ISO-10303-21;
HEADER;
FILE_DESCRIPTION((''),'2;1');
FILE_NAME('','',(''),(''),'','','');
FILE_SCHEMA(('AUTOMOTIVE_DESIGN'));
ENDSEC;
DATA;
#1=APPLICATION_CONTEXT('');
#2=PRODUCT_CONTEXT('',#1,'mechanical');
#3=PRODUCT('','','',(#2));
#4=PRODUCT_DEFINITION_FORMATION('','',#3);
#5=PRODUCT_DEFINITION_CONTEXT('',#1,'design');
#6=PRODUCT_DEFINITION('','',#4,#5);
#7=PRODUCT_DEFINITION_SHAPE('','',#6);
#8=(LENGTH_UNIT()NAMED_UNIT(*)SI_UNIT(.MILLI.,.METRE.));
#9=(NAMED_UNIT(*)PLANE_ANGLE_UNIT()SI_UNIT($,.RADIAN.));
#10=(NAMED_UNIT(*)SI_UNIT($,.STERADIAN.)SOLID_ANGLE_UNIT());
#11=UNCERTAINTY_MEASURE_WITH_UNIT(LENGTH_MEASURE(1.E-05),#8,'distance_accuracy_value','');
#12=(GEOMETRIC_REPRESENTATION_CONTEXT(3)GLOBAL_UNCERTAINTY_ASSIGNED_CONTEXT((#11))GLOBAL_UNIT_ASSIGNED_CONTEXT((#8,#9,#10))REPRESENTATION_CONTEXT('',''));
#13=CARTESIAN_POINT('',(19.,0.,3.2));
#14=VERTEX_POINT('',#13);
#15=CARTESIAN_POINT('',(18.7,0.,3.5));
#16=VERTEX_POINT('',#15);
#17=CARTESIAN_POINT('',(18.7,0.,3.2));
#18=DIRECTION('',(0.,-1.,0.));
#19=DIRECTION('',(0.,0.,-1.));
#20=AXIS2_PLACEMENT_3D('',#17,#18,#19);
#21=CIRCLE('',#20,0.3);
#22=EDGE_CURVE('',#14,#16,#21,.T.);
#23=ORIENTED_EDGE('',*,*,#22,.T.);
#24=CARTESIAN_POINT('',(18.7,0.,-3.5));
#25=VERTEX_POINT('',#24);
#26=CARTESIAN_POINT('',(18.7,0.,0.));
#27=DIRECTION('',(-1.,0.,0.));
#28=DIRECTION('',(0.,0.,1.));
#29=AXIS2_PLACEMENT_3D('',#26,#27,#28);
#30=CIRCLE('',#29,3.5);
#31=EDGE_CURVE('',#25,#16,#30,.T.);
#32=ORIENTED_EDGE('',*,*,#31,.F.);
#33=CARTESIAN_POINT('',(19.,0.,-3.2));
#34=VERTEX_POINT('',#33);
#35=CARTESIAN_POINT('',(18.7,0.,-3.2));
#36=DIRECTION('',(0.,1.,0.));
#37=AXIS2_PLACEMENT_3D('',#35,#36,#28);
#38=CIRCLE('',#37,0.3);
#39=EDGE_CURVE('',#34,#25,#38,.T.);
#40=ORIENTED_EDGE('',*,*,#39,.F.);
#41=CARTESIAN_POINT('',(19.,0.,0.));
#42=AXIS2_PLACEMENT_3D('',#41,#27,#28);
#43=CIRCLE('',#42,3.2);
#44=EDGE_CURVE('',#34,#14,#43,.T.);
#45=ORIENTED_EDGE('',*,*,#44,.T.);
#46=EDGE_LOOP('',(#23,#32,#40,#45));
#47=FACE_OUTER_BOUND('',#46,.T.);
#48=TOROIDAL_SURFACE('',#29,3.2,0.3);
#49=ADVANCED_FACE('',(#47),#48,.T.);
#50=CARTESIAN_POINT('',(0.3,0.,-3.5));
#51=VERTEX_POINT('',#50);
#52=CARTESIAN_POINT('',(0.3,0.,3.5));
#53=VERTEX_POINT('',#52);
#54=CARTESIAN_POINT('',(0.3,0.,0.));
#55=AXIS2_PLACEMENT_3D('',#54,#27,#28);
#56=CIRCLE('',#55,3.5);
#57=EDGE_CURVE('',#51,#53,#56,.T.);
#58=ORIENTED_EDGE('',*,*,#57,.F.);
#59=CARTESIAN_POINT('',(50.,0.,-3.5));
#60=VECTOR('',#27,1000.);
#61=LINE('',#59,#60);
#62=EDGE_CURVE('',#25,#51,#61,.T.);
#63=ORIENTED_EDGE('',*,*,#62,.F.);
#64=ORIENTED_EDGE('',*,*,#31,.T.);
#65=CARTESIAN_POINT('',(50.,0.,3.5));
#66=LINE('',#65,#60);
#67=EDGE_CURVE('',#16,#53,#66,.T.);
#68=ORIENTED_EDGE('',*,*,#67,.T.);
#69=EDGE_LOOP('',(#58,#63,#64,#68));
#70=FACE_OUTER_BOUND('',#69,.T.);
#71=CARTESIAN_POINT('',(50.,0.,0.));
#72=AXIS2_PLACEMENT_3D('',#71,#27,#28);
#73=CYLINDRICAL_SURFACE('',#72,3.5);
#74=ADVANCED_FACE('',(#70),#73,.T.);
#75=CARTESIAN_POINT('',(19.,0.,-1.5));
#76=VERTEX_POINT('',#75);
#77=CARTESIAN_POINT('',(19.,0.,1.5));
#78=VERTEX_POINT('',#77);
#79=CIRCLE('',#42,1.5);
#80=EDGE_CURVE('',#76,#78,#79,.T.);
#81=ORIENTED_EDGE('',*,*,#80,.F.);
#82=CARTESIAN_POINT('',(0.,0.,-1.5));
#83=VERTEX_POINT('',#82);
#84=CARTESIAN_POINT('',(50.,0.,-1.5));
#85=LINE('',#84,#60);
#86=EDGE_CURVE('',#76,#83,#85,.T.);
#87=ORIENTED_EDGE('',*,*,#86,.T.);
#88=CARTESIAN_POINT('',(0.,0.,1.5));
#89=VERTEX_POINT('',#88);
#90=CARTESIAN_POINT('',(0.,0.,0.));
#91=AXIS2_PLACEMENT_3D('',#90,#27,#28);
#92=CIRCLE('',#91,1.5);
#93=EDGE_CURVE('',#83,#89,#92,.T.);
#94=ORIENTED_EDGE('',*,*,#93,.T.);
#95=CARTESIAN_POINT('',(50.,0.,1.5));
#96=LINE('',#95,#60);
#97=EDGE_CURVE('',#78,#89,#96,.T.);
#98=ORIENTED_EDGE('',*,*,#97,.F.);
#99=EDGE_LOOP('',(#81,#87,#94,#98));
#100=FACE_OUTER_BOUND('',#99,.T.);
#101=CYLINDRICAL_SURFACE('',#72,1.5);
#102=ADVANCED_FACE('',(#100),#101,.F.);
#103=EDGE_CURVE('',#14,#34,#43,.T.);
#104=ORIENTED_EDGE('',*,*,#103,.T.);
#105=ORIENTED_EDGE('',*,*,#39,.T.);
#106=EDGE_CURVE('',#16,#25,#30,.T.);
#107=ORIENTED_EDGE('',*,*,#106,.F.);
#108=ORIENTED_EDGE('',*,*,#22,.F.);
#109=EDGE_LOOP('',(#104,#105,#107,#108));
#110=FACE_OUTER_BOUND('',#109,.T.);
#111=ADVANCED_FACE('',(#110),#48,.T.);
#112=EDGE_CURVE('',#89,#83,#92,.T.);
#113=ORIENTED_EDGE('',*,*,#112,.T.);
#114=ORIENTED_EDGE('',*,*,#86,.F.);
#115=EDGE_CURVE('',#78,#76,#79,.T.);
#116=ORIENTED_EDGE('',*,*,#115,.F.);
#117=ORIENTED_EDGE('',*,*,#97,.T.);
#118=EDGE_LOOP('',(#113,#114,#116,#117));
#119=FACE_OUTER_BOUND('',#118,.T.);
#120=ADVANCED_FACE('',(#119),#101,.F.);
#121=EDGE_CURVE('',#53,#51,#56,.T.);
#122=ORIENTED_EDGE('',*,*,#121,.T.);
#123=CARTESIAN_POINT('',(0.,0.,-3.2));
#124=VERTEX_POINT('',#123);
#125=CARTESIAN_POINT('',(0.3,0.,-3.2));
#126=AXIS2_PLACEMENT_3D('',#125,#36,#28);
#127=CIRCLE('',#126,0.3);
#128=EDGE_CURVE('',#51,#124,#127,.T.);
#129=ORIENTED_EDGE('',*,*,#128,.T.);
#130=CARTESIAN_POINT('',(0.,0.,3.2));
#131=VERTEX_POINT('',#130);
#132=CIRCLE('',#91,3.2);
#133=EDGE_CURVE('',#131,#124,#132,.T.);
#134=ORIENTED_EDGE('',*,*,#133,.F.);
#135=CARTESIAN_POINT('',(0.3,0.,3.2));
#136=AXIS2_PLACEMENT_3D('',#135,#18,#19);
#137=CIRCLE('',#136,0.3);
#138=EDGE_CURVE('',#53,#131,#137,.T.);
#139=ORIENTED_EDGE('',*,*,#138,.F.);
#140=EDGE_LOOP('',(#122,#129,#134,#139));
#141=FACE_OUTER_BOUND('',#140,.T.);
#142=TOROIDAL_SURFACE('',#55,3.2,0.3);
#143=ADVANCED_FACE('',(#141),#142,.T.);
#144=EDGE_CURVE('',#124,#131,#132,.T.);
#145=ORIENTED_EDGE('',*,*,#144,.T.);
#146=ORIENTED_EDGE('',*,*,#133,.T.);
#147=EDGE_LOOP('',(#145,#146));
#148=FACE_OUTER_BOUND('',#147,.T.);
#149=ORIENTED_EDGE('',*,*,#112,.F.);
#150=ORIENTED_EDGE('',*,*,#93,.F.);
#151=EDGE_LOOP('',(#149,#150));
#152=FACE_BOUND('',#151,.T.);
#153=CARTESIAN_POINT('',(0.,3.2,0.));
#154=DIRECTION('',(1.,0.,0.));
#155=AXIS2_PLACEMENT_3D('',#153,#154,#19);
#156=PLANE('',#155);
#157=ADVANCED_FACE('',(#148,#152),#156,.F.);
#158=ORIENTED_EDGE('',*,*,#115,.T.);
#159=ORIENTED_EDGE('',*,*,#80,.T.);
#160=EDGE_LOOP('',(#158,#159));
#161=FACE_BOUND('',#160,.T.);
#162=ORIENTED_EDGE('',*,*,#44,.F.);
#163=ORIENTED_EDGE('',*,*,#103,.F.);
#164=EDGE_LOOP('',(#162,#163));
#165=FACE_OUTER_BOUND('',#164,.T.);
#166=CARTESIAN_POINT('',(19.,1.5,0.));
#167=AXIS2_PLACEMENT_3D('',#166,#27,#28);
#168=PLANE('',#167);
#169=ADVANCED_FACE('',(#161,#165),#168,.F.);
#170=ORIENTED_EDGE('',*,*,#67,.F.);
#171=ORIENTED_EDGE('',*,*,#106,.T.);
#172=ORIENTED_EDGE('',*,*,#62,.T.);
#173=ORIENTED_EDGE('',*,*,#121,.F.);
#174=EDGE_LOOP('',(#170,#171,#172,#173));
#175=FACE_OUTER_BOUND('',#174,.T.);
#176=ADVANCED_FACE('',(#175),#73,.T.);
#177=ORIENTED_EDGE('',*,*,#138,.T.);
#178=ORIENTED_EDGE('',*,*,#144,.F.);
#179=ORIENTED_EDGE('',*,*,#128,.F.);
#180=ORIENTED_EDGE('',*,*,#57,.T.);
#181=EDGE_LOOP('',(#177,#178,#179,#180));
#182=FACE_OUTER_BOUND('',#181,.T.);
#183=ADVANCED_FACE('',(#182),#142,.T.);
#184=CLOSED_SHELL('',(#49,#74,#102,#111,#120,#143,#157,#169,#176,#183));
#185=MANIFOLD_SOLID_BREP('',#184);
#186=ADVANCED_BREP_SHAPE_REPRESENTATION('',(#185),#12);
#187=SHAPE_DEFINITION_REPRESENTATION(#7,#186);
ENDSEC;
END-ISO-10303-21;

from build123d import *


with BuildPart() as part:
    # Sketch1 → Revolve1 (revolve)
    with BuildSketch(Plane.XY, mode=Mode.PRIVATE) as revolve1_sk:
        with BuildLine():
            Line((0, 1.5), (19, 1.5))
            Line((19, 1.5), (19, 3.2))
            ThreePointArc((19, 3.2), (18.912132034, 3.412132034), (18.7, 3.5))
            Line((18.7, 3.5), (0.3, 3.5))
            ThreePointArc((0.3, 3.5), (0.087867966, 3.412132034), (0, 3.2))
            Line((0, 3.2), (0, 1.5))
        make_face()
    revolve(revolve1_sk.sketch.rotate(Axis((50, 0, 0), (-1, 0, 0)), 270), axis=Axis((50, 0, 0), (-1, 0, 0)))


solid = part.part
